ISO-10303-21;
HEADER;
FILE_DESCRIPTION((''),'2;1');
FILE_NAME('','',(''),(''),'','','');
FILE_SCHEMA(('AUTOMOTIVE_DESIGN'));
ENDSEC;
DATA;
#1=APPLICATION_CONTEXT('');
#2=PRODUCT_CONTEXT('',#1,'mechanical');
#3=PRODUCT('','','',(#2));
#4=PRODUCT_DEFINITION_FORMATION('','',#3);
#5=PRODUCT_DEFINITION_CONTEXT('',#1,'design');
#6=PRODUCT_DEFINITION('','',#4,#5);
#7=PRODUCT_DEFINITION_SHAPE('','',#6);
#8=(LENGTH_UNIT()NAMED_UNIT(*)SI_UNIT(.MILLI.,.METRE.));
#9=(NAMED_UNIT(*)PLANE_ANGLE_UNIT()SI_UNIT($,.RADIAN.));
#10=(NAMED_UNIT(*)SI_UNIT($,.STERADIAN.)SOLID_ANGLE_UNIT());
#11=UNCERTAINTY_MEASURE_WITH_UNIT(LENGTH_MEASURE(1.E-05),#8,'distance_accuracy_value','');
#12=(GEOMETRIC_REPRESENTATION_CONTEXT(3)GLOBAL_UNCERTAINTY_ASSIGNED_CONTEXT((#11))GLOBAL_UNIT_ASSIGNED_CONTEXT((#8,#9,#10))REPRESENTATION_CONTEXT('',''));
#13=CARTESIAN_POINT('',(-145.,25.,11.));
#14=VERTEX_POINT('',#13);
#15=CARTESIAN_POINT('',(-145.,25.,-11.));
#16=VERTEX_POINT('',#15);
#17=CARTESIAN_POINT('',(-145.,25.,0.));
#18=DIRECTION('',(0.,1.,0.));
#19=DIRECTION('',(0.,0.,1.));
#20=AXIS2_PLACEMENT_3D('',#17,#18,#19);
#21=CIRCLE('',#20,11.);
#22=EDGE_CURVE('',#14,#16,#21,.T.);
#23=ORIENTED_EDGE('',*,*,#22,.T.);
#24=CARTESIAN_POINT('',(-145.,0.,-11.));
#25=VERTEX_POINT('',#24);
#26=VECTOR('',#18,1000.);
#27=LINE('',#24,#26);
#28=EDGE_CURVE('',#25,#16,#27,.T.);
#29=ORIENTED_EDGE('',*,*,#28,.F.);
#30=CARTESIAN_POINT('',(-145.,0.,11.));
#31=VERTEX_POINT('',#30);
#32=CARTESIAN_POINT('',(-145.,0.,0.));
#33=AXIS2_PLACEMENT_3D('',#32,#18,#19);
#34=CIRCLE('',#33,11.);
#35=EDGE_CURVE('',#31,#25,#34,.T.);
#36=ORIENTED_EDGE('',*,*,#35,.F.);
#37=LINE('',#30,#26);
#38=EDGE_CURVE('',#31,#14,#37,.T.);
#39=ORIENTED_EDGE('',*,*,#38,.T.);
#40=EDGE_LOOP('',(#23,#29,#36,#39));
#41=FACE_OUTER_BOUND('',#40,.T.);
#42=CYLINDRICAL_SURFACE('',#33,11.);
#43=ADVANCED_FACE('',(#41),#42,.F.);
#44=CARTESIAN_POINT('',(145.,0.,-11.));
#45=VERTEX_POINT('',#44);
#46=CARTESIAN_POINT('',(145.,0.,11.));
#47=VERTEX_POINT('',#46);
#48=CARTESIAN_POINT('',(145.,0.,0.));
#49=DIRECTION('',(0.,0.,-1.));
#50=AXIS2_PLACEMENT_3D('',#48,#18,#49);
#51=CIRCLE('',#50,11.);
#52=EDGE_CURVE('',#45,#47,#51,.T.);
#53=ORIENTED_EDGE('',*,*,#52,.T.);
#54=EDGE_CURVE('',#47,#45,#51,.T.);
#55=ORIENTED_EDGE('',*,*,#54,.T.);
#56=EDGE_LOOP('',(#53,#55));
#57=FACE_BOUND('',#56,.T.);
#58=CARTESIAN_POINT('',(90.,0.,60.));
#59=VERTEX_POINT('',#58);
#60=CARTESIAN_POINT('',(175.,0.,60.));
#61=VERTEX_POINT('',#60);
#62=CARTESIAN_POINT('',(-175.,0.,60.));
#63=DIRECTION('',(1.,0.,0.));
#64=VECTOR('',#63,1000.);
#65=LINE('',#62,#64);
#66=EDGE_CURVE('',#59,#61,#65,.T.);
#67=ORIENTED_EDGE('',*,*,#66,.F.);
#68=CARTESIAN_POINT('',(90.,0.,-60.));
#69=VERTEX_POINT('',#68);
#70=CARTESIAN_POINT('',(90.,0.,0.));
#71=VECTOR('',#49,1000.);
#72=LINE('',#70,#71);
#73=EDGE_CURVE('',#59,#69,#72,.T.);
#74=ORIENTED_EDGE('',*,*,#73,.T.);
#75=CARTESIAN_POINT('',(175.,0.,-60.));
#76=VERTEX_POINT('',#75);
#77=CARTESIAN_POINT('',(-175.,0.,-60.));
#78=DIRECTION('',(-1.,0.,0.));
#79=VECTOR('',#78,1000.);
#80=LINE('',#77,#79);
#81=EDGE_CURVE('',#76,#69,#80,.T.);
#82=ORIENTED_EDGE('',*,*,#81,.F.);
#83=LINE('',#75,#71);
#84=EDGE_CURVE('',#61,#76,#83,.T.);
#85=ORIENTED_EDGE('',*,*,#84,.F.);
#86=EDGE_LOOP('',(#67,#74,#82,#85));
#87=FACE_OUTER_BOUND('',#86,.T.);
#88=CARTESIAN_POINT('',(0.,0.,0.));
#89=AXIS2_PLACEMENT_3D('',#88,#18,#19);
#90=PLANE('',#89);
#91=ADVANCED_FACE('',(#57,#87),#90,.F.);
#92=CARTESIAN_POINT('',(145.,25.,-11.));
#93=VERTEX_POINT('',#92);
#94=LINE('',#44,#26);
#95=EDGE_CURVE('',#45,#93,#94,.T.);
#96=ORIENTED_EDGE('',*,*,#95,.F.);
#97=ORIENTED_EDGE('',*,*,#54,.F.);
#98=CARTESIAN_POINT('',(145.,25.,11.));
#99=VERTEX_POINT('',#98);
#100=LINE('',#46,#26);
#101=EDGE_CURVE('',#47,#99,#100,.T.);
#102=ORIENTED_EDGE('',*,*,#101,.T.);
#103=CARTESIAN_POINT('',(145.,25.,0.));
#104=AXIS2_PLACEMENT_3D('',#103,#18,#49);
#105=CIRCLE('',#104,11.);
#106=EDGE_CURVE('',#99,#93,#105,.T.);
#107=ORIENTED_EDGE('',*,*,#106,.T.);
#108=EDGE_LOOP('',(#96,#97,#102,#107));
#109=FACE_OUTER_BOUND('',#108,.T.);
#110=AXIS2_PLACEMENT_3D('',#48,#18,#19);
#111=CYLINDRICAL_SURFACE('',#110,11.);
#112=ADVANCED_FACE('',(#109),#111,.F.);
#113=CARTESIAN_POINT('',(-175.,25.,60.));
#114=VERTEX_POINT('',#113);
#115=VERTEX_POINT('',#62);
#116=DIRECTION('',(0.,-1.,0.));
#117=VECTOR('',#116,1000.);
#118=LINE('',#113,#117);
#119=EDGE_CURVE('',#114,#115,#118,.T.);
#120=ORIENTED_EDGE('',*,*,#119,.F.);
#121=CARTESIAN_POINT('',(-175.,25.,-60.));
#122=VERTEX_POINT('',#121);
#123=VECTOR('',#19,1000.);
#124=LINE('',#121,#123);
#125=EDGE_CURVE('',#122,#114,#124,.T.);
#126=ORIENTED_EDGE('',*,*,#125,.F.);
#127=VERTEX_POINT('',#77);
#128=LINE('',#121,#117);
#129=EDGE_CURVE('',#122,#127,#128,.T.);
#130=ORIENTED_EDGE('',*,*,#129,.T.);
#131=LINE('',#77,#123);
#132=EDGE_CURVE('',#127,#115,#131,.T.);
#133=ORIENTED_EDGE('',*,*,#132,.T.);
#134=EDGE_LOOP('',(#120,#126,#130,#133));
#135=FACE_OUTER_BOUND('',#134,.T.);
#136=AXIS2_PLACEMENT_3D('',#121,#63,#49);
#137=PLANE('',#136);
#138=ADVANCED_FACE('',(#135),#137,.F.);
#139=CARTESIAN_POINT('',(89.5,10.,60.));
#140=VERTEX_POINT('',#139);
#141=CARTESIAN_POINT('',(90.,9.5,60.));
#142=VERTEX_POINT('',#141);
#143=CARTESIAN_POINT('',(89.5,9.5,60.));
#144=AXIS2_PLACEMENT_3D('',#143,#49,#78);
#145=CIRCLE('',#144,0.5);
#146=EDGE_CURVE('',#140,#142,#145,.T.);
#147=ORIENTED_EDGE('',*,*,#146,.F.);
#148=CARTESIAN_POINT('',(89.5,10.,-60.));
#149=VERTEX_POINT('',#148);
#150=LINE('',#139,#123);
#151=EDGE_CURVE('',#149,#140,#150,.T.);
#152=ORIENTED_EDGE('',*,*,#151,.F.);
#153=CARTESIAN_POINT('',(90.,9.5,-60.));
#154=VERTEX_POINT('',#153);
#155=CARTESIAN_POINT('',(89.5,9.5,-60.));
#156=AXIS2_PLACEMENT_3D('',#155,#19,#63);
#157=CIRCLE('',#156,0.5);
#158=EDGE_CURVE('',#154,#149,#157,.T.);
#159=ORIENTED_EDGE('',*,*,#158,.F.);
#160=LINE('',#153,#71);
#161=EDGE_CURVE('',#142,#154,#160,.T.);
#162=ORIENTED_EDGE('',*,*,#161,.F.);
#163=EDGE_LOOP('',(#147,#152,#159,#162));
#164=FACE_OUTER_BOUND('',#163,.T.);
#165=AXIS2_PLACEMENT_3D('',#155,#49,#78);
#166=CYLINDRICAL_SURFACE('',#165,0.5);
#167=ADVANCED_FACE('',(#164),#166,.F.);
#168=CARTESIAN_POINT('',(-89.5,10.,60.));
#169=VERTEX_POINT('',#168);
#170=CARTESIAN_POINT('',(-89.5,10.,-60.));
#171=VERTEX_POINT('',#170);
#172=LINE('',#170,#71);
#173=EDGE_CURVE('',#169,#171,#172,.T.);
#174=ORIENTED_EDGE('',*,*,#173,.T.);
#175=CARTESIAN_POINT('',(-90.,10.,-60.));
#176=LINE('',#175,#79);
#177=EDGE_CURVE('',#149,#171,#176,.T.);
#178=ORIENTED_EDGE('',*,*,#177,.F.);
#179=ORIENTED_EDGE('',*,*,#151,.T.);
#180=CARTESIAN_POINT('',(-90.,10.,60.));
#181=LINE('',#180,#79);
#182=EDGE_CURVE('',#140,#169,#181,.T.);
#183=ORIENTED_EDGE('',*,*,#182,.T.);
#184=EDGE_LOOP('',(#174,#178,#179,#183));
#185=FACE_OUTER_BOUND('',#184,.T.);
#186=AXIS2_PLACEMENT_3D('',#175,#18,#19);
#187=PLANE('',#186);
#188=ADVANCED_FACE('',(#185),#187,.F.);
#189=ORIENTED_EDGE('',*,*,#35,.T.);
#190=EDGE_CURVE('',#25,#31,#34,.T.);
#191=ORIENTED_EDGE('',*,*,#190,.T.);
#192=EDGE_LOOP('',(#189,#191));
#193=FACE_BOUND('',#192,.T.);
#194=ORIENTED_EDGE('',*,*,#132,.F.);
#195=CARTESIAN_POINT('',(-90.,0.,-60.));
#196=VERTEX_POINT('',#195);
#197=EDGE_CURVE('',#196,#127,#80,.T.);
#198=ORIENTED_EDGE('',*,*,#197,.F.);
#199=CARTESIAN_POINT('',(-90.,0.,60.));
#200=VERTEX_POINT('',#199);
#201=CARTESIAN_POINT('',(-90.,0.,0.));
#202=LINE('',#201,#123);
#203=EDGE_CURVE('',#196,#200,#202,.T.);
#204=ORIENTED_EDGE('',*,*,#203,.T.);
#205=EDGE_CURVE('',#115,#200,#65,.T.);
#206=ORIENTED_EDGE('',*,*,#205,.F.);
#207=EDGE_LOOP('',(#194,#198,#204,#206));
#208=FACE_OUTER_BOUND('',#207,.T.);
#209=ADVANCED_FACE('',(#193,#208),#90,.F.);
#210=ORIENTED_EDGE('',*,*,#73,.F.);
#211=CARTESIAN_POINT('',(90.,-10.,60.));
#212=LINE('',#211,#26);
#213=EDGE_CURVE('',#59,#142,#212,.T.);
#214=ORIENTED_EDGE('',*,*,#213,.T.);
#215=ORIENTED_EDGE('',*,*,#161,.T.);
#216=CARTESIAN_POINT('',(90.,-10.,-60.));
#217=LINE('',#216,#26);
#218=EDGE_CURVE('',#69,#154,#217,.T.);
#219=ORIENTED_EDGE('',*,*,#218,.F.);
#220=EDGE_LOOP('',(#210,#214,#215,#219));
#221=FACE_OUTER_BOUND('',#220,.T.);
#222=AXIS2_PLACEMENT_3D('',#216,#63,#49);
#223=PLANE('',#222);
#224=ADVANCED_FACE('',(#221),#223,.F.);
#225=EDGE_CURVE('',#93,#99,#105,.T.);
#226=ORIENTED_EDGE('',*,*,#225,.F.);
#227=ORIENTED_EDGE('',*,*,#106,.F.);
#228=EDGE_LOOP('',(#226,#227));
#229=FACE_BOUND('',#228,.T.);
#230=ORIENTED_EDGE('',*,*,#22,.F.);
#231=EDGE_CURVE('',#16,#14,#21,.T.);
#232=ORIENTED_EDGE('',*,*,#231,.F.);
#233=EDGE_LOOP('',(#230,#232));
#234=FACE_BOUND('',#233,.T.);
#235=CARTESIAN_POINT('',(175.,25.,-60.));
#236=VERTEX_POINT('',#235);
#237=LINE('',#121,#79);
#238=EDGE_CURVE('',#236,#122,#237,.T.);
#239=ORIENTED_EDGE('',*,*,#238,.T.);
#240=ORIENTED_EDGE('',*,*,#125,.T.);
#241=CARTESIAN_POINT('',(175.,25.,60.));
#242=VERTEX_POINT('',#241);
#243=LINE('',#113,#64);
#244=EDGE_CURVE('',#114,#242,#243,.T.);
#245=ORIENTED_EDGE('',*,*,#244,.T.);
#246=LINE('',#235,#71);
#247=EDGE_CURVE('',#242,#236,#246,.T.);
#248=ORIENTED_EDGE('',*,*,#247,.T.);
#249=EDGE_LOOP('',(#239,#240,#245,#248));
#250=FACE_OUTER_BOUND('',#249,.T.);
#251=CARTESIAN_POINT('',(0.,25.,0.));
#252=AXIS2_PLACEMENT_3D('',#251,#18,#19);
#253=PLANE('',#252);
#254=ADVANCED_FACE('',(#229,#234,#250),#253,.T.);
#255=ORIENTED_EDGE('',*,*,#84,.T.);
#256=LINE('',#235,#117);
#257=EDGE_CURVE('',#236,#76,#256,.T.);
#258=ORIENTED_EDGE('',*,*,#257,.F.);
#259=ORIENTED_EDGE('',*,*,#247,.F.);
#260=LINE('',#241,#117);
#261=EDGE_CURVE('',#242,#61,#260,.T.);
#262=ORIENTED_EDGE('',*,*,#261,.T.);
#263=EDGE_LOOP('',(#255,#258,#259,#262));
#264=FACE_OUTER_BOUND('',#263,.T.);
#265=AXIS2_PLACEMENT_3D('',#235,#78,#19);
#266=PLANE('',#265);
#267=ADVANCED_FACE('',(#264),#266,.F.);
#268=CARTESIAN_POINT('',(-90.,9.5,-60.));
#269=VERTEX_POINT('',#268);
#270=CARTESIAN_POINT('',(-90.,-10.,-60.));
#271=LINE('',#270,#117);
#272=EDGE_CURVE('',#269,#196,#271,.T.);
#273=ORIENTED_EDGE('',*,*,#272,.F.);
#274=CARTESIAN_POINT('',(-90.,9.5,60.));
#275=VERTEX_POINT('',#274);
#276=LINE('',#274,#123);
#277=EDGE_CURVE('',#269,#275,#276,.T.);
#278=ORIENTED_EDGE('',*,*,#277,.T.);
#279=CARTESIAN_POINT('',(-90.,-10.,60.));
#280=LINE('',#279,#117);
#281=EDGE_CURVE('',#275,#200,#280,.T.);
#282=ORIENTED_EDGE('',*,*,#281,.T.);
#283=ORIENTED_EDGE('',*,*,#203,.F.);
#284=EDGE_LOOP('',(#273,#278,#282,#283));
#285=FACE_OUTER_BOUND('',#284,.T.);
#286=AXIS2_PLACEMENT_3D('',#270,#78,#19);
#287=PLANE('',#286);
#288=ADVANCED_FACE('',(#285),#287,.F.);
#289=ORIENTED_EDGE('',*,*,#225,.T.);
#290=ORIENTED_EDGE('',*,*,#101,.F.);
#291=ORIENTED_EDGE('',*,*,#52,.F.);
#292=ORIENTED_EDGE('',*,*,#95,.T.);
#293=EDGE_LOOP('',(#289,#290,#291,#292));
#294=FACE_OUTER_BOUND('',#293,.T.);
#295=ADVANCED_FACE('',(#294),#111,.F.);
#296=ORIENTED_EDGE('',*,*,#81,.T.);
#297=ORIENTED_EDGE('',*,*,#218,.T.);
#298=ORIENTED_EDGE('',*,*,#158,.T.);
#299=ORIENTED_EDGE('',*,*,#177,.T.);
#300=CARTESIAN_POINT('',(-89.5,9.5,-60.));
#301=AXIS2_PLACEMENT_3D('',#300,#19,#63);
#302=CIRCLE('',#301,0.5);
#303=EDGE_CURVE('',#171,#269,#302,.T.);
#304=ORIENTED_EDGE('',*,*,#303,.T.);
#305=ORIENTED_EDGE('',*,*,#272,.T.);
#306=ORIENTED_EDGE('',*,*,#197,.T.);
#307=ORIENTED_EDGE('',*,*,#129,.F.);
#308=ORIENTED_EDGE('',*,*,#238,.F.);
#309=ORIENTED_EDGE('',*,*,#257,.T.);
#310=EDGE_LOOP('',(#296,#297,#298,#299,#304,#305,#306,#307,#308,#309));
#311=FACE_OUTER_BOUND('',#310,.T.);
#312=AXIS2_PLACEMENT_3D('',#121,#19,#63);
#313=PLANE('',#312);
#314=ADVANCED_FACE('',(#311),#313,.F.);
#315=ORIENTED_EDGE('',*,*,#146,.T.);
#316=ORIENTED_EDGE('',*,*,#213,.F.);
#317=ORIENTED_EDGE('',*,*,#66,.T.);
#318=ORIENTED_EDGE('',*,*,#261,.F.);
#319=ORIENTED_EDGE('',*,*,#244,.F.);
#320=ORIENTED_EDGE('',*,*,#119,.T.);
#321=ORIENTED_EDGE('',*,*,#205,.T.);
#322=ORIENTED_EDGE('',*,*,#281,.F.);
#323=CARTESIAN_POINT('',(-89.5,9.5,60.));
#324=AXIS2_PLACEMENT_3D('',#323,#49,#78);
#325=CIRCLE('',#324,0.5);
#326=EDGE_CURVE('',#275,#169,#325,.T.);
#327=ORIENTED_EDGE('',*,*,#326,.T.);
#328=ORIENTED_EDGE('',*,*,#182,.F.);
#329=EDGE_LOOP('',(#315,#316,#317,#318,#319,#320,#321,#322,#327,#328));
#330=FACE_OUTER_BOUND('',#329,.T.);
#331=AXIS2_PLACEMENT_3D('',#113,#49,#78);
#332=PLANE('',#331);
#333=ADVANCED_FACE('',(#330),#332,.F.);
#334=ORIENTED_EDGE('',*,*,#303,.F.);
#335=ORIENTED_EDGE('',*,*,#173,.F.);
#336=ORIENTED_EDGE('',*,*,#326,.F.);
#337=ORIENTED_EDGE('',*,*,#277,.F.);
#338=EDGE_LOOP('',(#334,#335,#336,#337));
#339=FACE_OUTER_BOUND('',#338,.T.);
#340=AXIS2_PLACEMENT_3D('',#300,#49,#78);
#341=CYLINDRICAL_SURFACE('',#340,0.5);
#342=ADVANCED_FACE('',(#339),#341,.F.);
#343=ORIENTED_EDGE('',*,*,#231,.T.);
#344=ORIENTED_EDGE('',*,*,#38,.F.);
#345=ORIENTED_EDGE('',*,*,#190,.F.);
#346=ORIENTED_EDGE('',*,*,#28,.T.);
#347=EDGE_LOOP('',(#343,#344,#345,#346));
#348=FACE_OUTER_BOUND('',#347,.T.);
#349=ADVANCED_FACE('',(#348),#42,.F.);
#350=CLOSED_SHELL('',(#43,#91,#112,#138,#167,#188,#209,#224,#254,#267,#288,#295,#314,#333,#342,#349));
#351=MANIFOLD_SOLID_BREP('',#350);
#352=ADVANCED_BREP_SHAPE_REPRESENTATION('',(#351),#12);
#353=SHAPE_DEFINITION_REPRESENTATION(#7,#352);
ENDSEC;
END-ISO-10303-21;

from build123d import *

# Parameters (mm, degrees)
SKETCH1_W           = 350
SKETCH1_H           = 120
BOSS_EXTRUDE1_DEPTH = 25
SKETCH2_W           = 180
SKETCH2_H           = 20
CUT_EXTRUDE1_DEPTH  = 214.658606192
SKETCH3_R           = 11
CUT_EXTRUDE2_DEPTH  = 25
FILLET1_R           = 0.5


with BuildPart() as part:
    # Sketch1 → Boss-Extrude1 (new body)
    with BuildSketch(Plane(origin=(0, 0, 0), x_dir=(1, 0, 0), z_dir=(0, 1, 0))):
        Rectangle(SKETCH1_W, SKETCH1_H)
    extrude(amount=BOSS_EXTRUDE1_DEPTH)

    # Sketch2 → Cut-Extrude1 (cut, through all)
    with BuildSketch(Plane.XY.offset(60)):
        Rectangle(SKETCH2_W, SKETCH2_H)
    extrude(amount=-CUT_EXTRUDE1_DEPTH, mode=Mode.SUBTRACT)

    # Sketch3 → Cut-Extrude2 (cut)
    with BuildSketch(Plane(origin=(0, 25, 0), x_dir=(1, 0, 0), z_dir=(0, 1, 0))):
        with Locations(Location((-145, 0, 0), (0, 0, 270))):
            Circle(SKETCH3_R)
        with Locations(Location((145, 0, 0), (0, 0, 90))):
            Circle(SKETCH3_R)
    extrude(amount=-CUT_EXTRUDE2_DEPTH, mode=Mode.SUBTRACT)

    # Fillet1
    fillet1_edges = [part.edges().sort_by_distance(p)[0] for p in [
        (90, 10, 0),
        (-90, 10, 0),
    ]]
    fillet(fillet1_edges, radius=FILLET1_R)


solid = part.part
